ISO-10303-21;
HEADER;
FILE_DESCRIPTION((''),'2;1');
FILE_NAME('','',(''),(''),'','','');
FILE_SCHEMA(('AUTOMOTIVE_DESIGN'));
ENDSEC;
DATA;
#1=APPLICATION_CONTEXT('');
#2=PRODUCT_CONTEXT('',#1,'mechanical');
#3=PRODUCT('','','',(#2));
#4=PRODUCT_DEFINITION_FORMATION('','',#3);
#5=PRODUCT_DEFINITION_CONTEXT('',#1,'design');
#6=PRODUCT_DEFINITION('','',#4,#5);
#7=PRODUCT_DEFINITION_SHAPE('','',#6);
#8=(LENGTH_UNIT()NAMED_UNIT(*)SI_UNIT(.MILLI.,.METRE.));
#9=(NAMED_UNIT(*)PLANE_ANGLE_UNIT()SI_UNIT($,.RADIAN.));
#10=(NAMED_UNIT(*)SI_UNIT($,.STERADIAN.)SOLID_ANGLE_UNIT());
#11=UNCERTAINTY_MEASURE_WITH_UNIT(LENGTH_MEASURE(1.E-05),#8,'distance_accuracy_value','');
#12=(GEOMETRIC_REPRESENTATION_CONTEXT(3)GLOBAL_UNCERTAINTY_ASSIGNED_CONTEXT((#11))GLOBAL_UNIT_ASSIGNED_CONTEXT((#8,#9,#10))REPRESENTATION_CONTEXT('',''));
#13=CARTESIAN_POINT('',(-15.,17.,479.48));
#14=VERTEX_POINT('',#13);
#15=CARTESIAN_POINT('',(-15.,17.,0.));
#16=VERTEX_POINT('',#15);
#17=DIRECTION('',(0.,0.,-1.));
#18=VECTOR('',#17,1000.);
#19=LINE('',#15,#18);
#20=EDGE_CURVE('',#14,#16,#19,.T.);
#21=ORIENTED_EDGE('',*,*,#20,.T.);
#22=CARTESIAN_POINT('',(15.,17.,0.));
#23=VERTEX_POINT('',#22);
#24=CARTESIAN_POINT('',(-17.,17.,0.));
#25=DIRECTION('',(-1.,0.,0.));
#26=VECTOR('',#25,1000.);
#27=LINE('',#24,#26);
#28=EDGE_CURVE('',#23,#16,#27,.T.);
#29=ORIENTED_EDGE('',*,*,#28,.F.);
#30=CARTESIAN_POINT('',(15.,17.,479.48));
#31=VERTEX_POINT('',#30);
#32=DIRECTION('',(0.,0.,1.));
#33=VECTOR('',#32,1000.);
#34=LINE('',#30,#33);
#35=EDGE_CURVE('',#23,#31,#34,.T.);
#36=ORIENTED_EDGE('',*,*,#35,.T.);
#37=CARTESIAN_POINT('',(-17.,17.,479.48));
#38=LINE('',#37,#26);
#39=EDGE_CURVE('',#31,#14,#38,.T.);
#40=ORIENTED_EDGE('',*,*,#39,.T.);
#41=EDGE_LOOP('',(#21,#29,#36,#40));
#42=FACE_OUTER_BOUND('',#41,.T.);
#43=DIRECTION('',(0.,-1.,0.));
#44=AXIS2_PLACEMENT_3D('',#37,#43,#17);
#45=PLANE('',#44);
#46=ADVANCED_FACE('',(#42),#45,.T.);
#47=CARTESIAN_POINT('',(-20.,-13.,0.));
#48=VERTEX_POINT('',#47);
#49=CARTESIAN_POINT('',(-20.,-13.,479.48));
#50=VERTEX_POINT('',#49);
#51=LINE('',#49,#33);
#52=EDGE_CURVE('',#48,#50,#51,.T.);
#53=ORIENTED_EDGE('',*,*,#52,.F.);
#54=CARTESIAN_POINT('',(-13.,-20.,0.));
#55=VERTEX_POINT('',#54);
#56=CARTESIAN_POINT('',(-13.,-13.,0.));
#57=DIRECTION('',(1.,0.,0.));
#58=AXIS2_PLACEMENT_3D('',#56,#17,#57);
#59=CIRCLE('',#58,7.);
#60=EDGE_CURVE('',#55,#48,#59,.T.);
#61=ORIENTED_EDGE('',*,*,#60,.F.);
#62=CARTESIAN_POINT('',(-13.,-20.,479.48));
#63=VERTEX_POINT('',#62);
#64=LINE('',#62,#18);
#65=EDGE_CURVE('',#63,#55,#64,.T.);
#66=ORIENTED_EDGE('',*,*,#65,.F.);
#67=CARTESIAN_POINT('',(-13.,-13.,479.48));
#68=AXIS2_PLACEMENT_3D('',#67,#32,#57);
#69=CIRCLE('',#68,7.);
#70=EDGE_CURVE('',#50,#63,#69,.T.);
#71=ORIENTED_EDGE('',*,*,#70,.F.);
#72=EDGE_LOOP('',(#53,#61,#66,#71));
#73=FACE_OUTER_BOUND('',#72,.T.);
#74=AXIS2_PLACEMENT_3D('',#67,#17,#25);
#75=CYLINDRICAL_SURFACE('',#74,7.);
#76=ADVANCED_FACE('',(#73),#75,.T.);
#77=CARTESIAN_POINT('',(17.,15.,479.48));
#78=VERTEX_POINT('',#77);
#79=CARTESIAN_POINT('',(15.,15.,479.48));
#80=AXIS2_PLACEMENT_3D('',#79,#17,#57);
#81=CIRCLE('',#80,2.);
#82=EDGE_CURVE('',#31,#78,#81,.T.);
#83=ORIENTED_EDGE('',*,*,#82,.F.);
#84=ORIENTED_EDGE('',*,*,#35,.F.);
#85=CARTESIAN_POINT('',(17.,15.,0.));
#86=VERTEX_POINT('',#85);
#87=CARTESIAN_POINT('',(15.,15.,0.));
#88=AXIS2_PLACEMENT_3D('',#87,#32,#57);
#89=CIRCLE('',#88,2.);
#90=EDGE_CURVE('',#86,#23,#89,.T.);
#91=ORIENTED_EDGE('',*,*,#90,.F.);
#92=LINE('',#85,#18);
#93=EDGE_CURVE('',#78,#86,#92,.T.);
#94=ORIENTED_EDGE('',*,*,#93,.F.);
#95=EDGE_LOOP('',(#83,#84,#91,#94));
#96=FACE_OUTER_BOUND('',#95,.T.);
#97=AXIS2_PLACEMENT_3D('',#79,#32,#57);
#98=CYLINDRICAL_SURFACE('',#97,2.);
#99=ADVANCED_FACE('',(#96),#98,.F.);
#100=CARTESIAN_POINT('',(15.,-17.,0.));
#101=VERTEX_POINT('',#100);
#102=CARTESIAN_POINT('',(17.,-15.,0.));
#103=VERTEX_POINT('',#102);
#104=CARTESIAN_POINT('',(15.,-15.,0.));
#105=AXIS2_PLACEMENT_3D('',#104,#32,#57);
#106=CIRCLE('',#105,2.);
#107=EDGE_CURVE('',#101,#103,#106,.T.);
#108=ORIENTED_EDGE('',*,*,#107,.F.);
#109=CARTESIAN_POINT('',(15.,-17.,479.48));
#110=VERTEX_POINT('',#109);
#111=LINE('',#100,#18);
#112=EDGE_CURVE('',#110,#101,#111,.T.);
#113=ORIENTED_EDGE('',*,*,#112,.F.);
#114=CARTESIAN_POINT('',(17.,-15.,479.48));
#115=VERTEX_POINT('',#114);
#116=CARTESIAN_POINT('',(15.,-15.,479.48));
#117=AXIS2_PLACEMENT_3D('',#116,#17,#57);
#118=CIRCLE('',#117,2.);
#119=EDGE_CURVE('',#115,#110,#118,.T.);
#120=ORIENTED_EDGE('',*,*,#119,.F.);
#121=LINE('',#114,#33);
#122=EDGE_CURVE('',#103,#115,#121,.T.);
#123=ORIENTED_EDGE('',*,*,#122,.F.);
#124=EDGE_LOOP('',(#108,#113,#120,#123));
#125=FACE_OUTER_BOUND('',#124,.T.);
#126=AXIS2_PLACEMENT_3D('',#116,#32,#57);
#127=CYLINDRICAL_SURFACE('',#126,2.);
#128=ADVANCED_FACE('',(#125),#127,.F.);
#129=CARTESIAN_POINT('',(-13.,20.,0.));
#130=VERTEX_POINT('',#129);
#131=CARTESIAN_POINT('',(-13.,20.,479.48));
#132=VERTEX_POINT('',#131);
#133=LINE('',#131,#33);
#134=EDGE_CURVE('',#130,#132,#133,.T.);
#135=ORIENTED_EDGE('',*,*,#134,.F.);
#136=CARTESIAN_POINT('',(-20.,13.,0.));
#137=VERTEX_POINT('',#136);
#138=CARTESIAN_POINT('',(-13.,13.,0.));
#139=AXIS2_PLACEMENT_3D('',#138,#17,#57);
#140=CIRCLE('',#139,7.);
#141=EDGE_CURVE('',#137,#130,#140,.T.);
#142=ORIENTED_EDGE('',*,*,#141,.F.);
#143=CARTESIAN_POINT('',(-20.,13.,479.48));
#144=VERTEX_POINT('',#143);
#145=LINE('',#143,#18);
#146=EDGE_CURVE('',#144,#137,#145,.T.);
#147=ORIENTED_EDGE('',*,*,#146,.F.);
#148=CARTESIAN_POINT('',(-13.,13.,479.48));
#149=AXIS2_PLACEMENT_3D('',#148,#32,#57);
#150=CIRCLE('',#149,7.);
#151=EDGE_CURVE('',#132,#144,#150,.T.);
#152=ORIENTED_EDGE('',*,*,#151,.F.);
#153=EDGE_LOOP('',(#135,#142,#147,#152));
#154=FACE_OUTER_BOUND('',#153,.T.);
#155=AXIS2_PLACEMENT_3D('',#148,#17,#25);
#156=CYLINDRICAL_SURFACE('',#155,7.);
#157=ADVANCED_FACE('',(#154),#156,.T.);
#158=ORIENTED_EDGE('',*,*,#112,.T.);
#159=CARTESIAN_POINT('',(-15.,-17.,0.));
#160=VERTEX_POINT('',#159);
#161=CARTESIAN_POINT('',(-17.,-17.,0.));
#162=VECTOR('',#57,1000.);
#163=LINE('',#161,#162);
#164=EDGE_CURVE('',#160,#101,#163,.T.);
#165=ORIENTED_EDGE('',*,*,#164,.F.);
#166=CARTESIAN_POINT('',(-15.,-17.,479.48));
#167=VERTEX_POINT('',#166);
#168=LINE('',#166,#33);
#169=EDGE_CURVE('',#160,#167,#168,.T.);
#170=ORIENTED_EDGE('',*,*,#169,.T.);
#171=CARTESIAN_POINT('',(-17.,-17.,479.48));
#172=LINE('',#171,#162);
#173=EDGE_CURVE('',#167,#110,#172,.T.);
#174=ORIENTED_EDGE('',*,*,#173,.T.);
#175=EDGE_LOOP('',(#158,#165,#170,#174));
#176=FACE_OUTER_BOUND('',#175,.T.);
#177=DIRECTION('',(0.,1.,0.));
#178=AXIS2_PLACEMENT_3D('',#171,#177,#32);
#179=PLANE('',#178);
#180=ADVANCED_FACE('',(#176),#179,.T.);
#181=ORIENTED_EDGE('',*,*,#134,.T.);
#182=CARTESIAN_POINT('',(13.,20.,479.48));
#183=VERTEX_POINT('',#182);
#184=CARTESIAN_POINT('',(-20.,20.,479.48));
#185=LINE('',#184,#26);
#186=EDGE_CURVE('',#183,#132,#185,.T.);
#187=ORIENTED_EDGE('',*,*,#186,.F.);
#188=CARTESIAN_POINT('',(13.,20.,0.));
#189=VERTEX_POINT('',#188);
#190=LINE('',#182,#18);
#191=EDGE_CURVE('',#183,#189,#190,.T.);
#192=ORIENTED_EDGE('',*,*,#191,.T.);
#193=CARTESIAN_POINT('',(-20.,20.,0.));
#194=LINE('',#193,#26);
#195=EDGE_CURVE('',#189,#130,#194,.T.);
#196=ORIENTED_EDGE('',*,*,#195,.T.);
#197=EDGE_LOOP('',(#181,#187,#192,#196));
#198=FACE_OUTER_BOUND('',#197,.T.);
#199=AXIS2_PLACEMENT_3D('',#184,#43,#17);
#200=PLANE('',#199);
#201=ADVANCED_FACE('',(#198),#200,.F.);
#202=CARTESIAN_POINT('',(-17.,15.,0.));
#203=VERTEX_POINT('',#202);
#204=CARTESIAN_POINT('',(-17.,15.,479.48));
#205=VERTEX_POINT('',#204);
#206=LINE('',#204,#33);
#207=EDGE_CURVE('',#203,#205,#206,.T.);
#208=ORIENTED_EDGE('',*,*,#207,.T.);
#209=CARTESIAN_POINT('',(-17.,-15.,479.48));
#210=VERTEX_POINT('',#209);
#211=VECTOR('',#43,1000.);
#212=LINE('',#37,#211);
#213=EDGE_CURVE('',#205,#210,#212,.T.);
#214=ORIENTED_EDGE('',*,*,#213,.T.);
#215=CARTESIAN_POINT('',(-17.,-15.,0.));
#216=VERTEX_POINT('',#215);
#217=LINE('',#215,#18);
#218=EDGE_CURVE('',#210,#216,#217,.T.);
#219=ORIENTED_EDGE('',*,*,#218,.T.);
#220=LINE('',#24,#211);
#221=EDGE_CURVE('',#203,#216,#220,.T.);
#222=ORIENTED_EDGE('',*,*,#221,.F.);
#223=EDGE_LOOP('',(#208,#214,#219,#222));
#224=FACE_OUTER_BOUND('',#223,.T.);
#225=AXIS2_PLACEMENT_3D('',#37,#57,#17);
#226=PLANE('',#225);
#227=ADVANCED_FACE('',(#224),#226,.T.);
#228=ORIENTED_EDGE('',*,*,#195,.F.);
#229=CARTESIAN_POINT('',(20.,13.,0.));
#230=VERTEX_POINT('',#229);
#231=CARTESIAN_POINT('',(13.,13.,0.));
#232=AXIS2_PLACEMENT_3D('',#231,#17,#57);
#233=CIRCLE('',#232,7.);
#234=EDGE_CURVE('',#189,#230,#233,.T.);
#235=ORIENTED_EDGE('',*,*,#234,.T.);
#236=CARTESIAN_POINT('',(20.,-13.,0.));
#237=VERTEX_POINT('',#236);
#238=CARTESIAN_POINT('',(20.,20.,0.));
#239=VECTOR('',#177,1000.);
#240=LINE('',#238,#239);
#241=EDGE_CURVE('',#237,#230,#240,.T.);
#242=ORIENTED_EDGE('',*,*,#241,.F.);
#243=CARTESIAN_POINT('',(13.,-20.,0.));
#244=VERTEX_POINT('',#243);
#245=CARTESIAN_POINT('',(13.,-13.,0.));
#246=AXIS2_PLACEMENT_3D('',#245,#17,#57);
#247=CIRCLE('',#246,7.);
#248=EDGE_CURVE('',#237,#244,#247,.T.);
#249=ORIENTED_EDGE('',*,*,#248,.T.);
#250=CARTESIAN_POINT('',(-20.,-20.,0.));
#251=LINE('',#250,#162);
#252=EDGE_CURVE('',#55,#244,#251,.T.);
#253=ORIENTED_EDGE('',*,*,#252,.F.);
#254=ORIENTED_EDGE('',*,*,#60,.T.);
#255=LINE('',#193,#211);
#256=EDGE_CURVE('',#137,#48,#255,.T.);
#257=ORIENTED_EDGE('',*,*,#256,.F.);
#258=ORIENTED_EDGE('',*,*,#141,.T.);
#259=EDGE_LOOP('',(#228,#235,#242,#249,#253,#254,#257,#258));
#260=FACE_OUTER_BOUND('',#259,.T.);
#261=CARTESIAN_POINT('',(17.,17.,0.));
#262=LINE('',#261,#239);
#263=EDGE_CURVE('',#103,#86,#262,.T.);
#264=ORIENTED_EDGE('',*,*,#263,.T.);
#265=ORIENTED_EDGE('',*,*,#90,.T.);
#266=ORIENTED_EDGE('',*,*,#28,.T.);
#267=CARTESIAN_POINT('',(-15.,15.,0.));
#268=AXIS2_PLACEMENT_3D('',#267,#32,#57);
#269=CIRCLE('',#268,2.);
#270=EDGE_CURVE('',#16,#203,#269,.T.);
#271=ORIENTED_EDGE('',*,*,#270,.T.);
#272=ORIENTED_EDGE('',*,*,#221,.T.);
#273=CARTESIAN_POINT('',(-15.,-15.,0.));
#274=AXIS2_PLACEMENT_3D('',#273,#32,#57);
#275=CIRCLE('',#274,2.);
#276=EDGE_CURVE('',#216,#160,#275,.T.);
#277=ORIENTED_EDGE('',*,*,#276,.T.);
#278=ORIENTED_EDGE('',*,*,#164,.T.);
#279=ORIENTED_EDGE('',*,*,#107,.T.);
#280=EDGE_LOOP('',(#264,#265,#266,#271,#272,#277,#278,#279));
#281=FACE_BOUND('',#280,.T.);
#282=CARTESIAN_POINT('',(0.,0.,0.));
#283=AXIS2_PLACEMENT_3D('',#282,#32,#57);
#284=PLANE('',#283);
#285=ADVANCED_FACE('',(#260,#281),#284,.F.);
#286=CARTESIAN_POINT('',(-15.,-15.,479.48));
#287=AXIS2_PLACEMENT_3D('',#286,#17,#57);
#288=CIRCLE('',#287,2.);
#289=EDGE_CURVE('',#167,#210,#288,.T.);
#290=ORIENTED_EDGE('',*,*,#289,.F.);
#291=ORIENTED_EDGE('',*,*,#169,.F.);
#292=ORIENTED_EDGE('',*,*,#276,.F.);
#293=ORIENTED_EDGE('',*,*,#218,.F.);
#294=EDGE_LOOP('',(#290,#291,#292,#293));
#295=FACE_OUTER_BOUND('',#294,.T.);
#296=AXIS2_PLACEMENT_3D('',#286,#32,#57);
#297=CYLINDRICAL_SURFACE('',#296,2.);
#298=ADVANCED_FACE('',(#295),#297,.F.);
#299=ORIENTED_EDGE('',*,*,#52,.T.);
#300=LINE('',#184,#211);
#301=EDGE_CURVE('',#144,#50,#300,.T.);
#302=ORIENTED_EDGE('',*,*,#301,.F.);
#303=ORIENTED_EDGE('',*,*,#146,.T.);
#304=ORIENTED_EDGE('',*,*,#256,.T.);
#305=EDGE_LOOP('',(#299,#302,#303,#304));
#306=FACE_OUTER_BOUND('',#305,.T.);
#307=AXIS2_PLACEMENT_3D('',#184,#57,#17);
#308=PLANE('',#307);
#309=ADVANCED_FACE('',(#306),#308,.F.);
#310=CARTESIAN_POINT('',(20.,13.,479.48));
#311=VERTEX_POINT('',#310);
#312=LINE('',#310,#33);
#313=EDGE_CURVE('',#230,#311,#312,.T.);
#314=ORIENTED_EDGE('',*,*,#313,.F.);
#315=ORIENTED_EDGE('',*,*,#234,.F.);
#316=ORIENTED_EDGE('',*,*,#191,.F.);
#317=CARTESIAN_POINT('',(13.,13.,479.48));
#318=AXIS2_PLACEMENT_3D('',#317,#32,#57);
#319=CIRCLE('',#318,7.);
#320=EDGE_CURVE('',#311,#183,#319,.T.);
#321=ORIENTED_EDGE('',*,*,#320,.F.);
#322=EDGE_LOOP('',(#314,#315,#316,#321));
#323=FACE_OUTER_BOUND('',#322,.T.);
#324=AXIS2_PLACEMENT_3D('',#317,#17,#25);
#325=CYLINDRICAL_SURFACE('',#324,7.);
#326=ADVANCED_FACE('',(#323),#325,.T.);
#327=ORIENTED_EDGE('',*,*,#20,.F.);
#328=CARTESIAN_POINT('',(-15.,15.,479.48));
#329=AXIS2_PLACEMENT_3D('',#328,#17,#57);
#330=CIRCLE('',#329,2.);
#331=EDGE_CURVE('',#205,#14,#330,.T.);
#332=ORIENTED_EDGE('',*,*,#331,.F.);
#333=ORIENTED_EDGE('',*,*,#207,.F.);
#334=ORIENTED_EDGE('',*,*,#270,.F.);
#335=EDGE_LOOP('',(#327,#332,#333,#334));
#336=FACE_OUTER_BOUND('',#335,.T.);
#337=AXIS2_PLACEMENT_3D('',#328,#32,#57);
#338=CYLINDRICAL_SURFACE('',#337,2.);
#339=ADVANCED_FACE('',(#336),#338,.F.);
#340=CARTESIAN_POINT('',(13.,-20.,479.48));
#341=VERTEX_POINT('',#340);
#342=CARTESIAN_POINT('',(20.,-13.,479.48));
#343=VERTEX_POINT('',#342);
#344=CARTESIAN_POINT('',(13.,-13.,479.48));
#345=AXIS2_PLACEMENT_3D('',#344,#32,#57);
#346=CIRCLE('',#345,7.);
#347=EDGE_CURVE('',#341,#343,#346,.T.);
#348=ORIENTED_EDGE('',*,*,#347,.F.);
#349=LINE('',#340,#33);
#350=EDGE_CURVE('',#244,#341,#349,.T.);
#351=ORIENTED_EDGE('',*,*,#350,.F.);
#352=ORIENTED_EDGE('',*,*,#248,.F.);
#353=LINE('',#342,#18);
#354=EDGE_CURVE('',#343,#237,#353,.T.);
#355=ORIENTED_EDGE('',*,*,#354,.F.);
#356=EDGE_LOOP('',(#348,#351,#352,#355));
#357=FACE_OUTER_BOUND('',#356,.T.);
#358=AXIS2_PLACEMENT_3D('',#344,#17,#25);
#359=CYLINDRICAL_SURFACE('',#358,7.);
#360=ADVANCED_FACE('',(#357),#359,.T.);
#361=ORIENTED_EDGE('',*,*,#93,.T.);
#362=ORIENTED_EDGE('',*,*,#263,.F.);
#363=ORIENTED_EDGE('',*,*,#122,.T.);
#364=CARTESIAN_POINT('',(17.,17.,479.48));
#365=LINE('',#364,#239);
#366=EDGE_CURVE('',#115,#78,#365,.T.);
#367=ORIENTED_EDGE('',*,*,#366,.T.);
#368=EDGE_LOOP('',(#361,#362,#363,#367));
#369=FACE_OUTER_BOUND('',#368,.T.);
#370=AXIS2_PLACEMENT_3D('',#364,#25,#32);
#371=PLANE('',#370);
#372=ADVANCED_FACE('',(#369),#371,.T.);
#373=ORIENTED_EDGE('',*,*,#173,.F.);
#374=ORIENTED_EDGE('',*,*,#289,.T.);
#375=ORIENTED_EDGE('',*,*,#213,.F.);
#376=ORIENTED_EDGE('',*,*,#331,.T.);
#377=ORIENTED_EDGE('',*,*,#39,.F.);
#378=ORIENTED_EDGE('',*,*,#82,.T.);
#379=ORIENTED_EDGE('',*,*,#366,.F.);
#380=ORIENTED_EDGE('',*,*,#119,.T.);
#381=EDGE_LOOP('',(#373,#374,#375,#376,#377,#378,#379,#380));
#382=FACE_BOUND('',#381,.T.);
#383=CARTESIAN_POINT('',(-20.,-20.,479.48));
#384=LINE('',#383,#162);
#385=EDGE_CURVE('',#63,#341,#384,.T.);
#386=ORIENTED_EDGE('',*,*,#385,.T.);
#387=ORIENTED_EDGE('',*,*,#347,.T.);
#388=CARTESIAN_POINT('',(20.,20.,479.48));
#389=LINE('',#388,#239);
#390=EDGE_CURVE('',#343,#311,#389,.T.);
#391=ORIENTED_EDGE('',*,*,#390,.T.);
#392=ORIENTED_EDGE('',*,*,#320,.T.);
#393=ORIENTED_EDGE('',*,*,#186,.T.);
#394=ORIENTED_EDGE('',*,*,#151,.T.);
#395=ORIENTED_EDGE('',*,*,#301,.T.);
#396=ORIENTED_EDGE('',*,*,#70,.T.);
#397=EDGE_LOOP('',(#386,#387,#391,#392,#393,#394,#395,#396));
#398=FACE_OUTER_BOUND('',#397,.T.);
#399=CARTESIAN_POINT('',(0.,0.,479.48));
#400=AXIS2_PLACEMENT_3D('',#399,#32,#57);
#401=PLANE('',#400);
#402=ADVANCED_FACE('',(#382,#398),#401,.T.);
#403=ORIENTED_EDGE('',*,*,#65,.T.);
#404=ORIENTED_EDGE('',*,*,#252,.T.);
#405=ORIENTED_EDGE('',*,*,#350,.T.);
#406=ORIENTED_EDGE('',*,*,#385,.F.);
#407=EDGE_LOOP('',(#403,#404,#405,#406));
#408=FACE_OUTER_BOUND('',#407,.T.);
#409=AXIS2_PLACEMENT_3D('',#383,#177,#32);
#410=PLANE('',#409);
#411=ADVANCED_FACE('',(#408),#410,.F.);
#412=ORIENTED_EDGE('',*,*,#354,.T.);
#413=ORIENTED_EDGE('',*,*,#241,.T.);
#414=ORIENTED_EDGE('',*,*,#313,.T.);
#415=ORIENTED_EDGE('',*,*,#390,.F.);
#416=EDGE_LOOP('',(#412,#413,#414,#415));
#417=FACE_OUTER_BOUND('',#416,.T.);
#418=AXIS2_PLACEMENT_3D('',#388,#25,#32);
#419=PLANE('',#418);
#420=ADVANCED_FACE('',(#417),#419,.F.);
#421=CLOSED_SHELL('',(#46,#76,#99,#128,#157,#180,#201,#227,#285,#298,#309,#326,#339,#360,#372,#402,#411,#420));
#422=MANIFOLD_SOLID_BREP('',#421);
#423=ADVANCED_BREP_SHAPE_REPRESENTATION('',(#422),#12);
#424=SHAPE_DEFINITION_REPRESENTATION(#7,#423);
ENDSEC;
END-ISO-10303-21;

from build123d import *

# Parameters (mm, degrees)
SKETCH1_W           = 40
SKETCH1_H           = 40
SKETCH1_W_2         = 34
SKETCH1_H_2         = 34
BOSS_EXTRUDE1_DEPTH = 479.48
FILLET1_R           = 2
FILLET2_R           = 7


with BuildPart() as part:
    # Sketch1 → Boss-Extrude1 (new body)
    with BuildSketch(Plane.XY):
        Rectangle(SKETCH1_W, SKETCH1_H)
        Rectangle(SKETCH1_W_2, SKETCH1_H_2, mode=Mode.SUBTRACT)
    extrude(amount=BOSS_EXTRUDE1_DEPTH)

    # Fillet1
    fillet1_edges = [part.edges().sort_by_distance(p)[0] for p in [
        (17, -17, 239.74),
        (17, 17, 239.74),
        (-17, 17, 239.74),
        (-17, -17, 239.74),
    ]]
    fillet(fillet1_edges, radius=FILLET1_R)

    # Fillet2
    fillet2_edges = [part.edges().sort_by_distance(p)[0] for p in [
        (20, -20, 239.74),
        (-20, -20, 239.74),
        (-20, 20, 239.74),
        (20, 20, 239.74),
    ]]
    fillet(fillet2_edges, radius=FILLET2_R)


solid = part.part
